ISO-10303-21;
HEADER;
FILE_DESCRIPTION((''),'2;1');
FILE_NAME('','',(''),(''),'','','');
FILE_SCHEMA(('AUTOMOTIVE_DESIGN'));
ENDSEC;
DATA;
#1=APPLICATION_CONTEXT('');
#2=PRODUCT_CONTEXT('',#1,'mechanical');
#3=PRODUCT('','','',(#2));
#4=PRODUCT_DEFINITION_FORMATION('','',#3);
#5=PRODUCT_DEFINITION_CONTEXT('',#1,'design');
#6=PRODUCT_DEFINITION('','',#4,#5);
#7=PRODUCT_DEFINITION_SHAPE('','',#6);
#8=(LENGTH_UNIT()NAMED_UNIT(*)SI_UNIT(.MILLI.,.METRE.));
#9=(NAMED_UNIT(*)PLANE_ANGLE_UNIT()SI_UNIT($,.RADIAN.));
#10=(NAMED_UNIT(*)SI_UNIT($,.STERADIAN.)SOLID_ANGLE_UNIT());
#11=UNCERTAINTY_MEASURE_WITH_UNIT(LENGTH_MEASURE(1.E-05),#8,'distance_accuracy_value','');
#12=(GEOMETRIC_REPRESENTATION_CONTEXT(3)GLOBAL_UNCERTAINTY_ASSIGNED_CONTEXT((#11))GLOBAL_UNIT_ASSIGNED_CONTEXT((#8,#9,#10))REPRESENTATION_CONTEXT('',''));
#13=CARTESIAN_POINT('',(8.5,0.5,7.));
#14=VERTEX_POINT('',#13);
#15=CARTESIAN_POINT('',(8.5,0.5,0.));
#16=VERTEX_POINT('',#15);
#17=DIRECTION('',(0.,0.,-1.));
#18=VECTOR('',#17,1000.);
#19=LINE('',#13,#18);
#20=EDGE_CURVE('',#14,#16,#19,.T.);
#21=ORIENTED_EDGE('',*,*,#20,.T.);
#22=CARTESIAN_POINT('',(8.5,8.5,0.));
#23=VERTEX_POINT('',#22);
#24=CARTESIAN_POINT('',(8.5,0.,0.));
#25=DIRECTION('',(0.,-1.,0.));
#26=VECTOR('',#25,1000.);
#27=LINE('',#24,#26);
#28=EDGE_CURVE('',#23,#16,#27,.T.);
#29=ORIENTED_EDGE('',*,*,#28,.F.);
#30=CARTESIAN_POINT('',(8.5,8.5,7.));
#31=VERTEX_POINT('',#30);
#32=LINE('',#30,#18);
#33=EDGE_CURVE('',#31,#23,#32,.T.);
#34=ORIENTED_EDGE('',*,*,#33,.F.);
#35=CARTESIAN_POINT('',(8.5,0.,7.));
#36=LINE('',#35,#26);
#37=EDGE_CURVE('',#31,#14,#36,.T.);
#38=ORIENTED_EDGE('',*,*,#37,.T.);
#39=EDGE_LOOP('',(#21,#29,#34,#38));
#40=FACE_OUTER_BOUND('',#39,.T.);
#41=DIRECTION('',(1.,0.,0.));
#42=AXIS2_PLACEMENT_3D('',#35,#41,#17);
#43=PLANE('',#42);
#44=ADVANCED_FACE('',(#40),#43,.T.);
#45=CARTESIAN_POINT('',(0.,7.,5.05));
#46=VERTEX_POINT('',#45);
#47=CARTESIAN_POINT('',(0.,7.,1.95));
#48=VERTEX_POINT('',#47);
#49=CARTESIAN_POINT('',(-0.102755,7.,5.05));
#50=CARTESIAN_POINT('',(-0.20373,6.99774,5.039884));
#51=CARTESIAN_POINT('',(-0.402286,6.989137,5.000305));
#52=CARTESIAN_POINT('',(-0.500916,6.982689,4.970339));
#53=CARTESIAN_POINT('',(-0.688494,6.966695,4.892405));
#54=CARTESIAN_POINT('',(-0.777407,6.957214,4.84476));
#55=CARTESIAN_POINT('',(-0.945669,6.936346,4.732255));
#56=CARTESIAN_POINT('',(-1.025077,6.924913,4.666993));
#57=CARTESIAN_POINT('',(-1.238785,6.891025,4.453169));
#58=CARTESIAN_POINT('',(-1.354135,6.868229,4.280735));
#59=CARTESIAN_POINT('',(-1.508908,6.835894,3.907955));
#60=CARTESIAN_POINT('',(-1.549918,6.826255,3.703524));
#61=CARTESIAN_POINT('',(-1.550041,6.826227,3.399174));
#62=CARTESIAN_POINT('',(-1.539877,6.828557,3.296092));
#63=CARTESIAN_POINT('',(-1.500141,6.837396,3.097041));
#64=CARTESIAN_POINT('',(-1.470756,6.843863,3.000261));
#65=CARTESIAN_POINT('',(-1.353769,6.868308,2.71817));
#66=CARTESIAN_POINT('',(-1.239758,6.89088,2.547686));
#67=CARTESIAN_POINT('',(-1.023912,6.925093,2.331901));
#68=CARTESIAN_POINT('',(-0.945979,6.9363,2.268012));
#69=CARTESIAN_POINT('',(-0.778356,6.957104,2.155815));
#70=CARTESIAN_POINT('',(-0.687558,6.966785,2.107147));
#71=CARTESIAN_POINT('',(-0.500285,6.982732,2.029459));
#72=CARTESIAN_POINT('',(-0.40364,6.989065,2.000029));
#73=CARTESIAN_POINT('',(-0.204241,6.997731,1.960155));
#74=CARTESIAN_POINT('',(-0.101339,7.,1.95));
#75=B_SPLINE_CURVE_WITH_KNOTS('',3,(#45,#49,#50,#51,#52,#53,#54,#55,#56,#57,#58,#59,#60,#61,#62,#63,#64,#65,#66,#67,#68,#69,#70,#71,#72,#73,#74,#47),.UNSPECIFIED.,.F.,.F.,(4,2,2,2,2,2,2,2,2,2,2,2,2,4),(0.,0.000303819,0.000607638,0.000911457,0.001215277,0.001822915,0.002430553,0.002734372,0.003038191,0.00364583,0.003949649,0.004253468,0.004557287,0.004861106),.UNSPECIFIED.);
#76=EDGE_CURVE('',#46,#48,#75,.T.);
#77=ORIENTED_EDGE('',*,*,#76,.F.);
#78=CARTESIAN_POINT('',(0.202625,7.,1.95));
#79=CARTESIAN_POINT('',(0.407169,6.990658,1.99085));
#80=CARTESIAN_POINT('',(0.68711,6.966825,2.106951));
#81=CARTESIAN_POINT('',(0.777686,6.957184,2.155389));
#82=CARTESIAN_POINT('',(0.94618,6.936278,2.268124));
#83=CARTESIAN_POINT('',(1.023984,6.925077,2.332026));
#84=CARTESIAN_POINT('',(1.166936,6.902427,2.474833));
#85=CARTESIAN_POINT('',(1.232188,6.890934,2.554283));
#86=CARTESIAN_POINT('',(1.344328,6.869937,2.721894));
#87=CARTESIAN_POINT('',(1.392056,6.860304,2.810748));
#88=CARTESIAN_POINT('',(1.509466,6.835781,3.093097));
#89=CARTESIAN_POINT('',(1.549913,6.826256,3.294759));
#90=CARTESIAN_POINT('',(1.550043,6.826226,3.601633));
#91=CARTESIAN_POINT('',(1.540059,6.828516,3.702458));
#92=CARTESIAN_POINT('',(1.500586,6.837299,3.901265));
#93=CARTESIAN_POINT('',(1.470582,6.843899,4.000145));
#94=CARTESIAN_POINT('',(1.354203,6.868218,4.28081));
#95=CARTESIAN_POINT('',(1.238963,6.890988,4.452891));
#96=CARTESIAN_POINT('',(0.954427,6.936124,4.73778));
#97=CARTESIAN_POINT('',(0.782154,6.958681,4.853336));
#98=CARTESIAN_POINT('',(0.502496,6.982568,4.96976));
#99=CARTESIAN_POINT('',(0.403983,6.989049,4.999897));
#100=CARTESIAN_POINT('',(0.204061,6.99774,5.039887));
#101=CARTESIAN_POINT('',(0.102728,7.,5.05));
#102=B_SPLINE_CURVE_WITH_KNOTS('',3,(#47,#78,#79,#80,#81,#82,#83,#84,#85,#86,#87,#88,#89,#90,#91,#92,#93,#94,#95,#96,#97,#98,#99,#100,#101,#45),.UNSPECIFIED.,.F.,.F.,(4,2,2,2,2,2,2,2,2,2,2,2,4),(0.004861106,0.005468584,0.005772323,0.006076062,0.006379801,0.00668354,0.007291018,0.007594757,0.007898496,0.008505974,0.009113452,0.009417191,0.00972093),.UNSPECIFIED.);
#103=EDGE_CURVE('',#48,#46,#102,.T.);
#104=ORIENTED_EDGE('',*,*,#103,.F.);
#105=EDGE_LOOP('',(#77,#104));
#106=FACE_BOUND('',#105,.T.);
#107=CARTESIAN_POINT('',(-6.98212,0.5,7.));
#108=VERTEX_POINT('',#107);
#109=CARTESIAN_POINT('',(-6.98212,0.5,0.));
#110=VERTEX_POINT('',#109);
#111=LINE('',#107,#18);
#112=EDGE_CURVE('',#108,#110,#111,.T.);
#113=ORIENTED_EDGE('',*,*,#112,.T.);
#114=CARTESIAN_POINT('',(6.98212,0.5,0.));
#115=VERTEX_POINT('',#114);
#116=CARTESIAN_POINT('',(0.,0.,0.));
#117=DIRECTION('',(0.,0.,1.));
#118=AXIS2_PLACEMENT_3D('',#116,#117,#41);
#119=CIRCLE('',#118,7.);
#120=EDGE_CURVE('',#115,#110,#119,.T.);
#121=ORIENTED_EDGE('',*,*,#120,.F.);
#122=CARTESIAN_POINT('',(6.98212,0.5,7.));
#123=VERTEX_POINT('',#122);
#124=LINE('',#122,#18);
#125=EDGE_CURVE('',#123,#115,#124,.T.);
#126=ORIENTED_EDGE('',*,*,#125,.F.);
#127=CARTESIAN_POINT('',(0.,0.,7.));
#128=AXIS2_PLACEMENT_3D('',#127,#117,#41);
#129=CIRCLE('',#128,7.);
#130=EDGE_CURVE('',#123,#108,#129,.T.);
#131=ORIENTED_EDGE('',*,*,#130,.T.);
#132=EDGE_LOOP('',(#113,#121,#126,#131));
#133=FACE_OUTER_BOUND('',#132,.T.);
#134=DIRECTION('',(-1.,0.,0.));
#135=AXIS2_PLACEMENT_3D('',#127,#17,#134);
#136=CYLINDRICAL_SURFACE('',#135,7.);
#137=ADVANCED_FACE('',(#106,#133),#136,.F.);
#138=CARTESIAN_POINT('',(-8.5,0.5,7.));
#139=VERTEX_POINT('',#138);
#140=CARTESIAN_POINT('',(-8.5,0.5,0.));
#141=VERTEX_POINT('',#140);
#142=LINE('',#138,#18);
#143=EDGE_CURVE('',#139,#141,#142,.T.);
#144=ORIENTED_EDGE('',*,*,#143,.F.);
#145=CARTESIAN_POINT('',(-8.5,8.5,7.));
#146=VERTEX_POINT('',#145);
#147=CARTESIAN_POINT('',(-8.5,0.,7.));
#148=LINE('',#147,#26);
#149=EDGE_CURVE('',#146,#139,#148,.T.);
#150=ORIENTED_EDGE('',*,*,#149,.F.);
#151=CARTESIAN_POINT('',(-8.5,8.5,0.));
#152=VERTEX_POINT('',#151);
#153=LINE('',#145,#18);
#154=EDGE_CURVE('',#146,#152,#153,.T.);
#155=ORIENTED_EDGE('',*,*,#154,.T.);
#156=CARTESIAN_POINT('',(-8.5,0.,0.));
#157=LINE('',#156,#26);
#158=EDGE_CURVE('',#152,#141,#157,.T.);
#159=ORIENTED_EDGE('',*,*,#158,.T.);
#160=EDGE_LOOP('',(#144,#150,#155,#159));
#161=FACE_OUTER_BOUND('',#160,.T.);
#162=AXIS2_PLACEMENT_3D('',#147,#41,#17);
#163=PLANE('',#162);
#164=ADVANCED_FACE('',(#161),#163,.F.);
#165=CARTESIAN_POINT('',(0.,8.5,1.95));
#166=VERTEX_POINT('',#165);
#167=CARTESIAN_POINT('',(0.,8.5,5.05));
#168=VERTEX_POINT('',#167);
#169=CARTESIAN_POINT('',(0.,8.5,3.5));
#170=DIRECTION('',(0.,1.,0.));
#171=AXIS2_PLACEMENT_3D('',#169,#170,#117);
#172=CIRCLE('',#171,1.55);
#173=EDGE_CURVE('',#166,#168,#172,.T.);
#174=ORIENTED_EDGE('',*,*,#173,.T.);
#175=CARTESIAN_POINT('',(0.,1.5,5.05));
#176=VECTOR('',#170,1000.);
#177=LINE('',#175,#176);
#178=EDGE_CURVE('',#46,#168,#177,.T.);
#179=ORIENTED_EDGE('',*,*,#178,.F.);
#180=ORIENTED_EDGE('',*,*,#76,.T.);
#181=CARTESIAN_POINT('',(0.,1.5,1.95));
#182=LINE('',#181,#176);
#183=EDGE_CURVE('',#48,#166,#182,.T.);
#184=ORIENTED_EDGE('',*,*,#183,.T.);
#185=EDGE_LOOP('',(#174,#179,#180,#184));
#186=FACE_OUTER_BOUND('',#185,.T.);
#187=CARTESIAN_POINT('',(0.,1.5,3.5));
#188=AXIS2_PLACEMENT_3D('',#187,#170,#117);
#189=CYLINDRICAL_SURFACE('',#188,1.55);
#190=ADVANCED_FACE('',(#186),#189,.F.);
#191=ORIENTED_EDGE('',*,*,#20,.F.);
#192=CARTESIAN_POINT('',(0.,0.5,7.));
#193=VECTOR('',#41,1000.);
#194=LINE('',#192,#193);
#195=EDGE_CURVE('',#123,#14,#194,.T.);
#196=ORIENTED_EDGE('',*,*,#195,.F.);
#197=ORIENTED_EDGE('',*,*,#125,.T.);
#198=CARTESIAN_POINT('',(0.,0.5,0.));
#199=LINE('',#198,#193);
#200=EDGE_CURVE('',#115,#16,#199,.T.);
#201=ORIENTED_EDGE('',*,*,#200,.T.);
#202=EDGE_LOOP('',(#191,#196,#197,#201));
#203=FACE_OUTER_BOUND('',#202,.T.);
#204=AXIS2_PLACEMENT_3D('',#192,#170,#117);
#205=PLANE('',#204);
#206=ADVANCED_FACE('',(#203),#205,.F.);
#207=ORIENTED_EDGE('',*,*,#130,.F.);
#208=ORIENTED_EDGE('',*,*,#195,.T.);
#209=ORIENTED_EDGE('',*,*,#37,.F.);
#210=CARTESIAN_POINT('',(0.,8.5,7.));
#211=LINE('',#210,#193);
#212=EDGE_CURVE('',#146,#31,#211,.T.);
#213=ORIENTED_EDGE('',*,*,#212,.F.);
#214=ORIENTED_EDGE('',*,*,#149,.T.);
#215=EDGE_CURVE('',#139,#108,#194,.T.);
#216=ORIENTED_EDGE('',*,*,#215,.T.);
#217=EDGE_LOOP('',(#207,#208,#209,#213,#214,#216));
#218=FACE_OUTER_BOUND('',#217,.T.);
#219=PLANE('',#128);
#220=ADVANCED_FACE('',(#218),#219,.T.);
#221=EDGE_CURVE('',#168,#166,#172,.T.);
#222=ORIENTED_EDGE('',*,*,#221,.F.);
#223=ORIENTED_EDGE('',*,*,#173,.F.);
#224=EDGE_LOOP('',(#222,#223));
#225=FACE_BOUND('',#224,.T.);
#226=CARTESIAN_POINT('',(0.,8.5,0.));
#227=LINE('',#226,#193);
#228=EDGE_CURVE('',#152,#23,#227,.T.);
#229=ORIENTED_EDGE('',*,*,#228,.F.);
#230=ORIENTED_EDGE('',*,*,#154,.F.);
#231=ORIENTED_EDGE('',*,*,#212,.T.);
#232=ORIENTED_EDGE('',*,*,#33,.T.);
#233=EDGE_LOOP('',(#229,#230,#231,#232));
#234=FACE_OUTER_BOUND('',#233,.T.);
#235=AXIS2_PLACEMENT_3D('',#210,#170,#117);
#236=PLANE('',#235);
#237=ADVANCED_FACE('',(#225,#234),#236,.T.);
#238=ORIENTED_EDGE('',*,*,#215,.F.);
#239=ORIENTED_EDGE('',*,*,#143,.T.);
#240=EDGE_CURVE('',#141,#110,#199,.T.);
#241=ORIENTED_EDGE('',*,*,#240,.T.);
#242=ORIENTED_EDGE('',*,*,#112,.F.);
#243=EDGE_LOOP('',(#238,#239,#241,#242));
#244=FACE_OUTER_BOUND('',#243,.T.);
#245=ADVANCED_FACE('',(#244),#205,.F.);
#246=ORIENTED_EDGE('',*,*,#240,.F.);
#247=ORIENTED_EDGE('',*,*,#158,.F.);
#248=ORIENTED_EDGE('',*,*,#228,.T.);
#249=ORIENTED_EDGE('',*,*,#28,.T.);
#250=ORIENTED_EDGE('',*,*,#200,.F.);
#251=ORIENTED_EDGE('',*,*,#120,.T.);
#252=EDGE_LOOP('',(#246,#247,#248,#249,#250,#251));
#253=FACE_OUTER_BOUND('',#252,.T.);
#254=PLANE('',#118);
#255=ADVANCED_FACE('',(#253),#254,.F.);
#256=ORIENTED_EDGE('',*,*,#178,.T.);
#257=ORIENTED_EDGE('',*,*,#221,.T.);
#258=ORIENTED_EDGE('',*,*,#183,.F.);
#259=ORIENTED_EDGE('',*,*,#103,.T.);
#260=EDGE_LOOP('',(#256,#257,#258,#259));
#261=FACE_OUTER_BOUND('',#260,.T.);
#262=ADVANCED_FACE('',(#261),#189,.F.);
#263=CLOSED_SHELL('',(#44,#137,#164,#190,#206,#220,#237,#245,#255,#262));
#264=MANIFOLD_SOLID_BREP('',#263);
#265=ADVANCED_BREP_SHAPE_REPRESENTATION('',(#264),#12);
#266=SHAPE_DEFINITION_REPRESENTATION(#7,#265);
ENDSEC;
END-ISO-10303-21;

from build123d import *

# Parameters (mm, degrees)
EXTRUDE_1_DEPTH     = 7
SKETCH_2_R          = 1.55
CUT_EXTRUDE_1_DEPTH = 7


with BuildPart() as part:
    # 草图1 → 凸台-拉伸1 (new body)
    with BuildSketch(Plane.XY):
        with BuildLine():
            Line((8.5, 8.5), (-8.5, 8.5))
            Line((-8.5, 8.5), (-8.5, 0.5))
            Line((-8.5, 0.5), (-6.982120022, 0.5))
            ThreePointArc((-6.982120022, 0.5), (0, 7), (6.982120022, 0.5))
            Line((6.982120022, 0.5), (8.5, 0.5))
            Line((8.5, 0.5), (8.5, 8.5))
        make_face()
    extrude(amount=EXTRUDE_1_DEPTH)

    # 草图2 → 切除-拉伸1 (cut)
    with BuildSketch(Plane(origin=(0, 8.5, 0), x_dir=(1, 0, 0), z_dir=(0, 1, 0))):
        with Locations(Location((0, -3.5, 0), (0, 0, 270))):
            Circle(SKETCH_2_R)
    extrude(amount=-CUT_EXTRUDE_1_DEPTH, mode=Mode.SUBTRACT)


solid = part.part
